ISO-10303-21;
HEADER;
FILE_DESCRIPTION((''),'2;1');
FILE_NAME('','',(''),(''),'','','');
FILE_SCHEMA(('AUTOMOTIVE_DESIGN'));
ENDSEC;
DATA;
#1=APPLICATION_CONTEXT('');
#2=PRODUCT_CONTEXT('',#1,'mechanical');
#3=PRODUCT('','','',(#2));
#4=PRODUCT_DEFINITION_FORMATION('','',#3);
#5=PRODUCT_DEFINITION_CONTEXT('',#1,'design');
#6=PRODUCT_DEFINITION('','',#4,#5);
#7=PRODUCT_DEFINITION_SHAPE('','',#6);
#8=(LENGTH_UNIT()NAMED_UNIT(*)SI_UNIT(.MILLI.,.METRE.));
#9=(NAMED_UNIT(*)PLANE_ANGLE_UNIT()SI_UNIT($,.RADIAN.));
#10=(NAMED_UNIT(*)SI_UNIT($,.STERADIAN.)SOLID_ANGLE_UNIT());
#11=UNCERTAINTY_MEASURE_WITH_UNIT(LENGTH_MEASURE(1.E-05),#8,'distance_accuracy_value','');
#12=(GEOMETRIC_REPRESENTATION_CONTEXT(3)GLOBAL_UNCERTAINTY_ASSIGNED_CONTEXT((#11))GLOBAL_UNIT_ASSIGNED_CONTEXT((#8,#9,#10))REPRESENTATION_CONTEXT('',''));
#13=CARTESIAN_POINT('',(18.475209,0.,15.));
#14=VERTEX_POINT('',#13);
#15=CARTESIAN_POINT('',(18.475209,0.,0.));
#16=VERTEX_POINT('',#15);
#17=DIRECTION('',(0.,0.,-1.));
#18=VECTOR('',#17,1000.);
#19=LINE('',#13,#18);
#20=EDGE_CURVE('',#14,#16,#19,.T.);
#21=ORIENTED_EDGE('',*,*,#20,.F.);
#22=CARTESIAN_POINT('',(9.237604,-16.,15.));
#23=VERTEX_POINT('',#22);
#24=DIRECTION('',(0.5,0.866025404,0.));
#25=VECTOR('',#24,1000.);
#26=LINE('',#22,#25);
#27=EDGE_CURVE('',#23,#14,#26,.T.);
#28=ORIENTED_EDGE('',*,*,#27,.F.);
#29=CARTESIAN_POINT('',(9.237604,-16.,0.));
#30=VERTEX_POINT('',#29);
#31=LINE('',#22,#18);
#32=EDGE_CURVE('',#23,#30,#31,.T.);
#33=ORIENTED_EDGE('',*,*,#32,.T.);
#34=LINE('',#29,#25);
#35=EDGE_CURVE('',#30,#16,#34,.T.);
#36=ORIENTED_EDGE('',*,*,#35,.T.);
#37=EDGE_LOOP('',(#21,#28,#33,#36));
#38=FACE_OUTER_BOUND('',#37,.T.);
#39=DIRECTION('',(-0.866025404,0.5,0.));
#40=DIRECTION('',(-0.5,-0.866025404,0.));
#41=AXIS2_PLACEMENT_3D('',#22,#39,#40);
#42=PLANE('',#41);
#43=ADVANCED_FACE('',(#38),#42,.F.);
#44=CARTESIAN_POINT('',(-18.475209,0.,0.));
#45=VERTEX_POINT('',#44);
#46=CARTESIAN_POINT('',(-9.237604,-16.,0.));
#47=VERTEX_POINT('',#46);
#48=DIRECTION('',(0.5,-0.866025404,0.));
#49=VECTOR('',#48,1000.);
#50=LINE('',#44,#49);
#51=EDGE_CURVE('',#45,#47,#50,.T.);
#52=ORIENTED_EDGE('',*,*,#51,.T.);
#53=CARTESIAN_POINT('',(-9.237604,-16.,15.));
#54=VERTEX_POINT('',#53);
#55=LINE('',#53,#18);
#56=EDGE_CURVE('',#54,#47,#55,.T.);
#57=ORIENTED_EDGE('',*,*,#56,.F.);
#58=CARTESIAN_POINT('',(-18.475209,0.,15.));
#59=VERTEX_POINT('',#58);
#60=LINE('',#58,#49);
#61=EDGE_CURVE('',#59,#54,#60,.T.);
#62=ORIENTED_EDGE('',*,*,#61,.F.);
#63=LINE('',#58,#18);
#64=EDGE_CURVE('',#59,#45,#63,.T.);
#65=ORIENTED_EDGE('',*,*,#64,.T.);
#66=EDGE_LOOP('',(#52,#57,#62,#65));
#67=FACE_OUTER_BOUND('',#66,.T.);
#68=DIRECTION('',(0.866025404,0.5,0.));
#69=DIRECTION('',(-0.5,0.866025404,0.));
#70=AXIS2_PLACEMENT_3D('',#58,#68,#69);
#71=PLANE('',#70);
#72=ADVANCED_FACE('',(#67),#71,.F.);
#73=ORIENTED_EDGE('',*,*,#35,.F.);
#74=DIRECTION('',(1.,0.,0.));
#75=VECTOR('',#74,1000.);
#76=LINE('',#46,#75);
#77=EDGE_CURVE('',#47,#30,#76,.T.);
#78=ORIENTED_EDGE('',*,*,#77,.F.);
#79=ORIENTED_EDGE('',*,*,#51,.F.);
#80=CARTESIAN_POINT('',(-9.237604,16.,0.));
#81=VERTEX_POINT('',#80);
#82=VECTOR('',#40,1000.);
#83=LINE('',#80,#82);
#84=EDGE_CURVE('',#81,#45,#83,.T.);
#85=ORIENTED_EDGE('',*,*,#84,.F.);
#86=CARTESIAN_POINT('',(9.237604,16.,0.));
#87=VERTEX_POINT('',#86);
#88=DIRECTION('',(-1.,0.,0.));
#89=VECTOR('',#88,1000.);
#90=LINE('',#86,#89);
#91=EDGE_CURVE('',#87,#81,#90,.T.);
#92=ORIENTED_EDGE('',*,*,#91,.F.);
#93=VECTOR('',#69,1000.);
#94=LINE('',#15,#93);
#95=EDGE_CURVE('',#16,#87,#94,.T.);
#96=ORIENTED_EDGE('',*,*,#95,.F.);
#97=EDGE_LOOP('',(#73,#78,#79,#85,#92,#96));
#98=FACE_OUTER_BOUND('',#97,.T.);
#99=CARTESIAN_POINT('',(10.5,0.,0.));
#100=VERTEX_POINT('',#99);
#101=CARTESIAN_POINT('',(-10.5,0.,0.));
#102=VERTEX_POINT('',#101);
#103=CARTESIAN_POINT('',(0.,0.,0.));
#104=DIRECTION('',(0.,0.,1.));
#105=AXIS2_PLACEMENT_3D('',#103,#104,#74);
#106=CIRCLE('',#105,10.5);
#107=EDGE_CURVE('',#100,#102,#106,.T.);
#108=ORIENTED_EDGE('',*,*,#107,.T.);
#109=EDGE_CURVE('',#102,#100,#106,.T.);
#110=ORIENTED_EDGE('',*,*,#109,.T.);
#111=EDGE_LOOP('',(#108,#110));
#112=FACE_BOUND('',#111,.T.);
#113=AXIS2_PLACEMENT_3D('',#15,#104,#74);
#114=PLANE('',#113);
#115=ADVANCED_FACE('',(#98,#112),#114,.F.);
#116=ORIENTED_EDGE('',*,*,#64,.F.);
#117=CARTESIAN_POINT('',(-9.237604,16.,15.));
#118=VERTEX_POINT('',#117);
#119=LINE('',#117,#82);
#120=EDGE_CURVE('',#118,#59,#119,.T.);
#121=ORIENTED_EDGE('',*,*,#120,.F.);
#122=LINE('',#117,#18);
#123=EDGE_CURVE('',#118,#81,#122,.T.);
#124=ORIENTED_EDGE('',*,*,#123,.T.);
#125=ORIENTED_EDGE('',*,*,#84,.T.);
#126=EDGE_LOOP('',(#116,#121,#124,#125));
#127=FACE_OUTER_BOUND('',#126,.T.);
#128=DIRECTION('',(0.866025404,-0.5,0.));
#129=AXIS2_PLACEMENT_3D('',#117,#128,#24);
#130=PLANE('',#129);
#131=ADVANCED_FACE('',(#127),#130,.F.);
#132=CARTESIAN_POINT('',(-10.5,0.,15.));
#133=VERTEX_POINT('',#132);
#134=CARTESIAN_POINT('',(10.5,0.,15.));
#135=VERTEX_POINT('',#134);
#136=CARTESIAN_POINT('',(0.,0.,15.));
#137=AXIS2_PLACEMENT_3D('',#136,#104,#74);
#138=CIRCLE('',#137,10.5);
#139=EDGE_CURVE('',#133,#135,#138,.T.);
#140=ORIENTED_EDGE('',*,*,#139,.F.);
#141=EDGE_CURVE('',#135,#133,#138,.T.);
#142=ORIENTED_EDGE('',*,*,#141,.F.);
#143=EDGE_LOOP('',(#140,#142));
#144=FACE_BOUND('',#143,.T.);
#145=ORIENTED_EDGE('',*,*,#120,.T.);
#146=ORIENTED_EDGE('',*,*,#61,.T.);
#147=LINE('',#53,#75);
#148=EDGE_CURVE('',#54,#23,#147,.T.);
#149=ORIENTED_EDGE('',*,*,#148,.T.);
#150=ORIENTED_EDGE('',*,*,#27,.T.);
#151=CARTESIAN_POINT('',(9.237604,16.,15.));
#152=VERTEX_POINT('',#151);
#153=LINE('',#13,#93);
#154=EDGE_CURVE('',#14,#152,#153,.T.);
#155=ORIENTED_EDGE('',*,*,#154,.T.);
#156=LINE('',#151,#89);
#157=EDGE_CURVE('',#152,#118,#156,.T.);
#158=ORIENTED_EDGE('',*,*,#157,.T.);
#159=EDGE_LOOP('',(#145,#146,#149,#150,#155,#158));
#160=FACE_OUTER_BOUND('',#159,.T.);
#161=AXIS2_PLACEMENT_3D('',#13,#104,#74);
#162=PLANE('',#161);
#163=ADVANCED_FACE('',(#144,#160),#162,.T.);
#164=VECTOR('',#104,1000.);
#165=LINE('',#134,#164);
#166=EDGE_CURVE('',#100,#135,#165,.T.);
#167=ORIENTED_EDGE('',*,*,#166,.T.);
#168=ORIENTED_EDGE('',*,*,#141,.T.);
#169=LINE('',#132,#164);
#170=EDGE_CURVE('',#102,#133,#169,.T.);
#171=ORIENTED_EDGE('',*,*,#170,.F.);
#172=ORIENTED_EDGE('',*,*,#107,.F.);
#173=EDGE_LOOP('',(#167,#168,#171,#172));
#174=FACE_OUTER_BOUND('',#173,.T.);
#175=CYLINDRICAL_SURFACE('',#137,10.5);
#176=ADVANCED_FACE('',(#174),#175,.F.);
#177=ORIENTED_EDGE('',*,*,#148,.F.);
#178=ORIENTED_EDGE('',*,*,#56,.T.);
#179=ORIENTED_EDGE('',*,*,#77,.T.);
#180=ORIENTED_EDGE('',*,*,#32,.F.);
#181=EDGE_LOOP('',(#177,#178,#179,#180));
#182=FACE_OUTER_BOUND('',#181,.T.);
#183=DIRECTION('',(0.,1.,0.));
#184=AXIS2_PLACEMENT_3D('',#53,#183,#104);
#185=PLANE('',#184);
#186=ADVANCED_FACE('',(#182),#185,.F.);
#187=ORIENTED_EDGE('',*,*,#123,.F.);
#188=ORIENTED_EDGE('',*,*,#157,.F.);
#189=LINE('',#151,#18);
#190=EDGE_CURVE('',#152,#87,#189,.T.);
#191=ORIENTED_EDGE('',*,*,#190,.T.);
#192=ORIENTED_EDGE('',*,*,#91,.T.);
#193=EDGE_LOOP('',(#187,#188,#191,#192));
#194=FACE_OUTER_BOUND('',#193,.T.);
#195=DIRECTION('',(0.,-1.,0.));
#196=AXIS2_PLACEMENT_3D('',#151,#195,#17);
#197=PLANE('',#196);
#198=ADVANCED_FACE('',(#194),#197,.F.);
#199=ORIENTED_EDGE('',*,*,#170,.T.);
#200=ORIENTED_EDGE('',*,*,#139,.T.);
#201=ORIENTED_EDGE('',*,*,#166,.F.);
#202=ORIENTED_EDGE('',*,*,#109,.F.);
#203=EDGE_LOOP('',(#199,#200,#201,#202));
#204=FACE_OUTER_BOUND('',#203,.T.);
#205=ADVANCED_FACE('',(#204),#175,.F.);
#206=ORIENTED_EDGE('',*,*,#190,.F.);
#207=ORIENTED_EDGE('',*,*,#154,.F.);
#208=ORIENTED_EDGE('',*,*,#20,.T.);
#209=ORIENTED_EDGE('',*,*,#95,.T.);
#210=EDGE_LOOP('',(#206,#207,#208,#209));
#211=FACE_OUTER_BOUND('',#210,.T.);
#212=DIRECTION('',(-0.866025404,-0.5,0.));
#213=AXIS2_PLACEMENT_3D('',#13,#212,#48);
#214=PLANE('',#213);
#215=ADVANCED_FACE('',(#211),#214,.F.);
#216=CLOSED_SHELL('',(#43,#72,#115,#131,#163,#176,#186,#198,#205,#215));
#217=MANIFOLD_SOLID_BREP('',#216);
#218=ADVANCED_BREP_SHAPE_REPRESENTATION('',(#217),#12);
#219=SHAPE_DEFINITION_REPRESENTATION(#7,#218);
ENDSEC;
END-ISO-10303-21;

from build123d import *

# Parameters (mm, degrees)
BOSS_EXTRUDE1_DEPTH    = 15
M24_TAPPED_HOLE1_D     = 21
M24_TAPPED_HOLE1_DEPTH = 57
M24_TAPPED_HOLE1_TIP   = 6.3090365


with BuildPart() as part:
    # Sketch1 → Boss-Extrude1 (new body)
    with BuildSketch(Plane.XY):
        Polygon((18.475208614, 0), (9.237604307, 16), (-9.237604307, 16), (-18.475208614, 0), (-9.237604307, -16), (9.237604307, -16), align=None)
    extrude(amount=BOSS_EXTRUDE1_DEPTH)

    # M24 Tapped Hole1
    with Locations(Plane.XY.offset(15)):
        with Locations((0, 0)):
            Hole(M24_TAPPED_HOLE1_D / 2, depth=M24_TAPPED_HOLE1_DEPTH)
            with Locations((0, 0, -(M24_TAPPED_HOLE1_DEPTH + M24_TAPPED_HOLE1_TIP / 2))):  # 118° drill point
                Cone(0, M24_TAPPED_HOLE1_D / 2, M24_TAPPED_HOLE1_TIP, mode=Mode.SUBTRACT)


solid = part.part
